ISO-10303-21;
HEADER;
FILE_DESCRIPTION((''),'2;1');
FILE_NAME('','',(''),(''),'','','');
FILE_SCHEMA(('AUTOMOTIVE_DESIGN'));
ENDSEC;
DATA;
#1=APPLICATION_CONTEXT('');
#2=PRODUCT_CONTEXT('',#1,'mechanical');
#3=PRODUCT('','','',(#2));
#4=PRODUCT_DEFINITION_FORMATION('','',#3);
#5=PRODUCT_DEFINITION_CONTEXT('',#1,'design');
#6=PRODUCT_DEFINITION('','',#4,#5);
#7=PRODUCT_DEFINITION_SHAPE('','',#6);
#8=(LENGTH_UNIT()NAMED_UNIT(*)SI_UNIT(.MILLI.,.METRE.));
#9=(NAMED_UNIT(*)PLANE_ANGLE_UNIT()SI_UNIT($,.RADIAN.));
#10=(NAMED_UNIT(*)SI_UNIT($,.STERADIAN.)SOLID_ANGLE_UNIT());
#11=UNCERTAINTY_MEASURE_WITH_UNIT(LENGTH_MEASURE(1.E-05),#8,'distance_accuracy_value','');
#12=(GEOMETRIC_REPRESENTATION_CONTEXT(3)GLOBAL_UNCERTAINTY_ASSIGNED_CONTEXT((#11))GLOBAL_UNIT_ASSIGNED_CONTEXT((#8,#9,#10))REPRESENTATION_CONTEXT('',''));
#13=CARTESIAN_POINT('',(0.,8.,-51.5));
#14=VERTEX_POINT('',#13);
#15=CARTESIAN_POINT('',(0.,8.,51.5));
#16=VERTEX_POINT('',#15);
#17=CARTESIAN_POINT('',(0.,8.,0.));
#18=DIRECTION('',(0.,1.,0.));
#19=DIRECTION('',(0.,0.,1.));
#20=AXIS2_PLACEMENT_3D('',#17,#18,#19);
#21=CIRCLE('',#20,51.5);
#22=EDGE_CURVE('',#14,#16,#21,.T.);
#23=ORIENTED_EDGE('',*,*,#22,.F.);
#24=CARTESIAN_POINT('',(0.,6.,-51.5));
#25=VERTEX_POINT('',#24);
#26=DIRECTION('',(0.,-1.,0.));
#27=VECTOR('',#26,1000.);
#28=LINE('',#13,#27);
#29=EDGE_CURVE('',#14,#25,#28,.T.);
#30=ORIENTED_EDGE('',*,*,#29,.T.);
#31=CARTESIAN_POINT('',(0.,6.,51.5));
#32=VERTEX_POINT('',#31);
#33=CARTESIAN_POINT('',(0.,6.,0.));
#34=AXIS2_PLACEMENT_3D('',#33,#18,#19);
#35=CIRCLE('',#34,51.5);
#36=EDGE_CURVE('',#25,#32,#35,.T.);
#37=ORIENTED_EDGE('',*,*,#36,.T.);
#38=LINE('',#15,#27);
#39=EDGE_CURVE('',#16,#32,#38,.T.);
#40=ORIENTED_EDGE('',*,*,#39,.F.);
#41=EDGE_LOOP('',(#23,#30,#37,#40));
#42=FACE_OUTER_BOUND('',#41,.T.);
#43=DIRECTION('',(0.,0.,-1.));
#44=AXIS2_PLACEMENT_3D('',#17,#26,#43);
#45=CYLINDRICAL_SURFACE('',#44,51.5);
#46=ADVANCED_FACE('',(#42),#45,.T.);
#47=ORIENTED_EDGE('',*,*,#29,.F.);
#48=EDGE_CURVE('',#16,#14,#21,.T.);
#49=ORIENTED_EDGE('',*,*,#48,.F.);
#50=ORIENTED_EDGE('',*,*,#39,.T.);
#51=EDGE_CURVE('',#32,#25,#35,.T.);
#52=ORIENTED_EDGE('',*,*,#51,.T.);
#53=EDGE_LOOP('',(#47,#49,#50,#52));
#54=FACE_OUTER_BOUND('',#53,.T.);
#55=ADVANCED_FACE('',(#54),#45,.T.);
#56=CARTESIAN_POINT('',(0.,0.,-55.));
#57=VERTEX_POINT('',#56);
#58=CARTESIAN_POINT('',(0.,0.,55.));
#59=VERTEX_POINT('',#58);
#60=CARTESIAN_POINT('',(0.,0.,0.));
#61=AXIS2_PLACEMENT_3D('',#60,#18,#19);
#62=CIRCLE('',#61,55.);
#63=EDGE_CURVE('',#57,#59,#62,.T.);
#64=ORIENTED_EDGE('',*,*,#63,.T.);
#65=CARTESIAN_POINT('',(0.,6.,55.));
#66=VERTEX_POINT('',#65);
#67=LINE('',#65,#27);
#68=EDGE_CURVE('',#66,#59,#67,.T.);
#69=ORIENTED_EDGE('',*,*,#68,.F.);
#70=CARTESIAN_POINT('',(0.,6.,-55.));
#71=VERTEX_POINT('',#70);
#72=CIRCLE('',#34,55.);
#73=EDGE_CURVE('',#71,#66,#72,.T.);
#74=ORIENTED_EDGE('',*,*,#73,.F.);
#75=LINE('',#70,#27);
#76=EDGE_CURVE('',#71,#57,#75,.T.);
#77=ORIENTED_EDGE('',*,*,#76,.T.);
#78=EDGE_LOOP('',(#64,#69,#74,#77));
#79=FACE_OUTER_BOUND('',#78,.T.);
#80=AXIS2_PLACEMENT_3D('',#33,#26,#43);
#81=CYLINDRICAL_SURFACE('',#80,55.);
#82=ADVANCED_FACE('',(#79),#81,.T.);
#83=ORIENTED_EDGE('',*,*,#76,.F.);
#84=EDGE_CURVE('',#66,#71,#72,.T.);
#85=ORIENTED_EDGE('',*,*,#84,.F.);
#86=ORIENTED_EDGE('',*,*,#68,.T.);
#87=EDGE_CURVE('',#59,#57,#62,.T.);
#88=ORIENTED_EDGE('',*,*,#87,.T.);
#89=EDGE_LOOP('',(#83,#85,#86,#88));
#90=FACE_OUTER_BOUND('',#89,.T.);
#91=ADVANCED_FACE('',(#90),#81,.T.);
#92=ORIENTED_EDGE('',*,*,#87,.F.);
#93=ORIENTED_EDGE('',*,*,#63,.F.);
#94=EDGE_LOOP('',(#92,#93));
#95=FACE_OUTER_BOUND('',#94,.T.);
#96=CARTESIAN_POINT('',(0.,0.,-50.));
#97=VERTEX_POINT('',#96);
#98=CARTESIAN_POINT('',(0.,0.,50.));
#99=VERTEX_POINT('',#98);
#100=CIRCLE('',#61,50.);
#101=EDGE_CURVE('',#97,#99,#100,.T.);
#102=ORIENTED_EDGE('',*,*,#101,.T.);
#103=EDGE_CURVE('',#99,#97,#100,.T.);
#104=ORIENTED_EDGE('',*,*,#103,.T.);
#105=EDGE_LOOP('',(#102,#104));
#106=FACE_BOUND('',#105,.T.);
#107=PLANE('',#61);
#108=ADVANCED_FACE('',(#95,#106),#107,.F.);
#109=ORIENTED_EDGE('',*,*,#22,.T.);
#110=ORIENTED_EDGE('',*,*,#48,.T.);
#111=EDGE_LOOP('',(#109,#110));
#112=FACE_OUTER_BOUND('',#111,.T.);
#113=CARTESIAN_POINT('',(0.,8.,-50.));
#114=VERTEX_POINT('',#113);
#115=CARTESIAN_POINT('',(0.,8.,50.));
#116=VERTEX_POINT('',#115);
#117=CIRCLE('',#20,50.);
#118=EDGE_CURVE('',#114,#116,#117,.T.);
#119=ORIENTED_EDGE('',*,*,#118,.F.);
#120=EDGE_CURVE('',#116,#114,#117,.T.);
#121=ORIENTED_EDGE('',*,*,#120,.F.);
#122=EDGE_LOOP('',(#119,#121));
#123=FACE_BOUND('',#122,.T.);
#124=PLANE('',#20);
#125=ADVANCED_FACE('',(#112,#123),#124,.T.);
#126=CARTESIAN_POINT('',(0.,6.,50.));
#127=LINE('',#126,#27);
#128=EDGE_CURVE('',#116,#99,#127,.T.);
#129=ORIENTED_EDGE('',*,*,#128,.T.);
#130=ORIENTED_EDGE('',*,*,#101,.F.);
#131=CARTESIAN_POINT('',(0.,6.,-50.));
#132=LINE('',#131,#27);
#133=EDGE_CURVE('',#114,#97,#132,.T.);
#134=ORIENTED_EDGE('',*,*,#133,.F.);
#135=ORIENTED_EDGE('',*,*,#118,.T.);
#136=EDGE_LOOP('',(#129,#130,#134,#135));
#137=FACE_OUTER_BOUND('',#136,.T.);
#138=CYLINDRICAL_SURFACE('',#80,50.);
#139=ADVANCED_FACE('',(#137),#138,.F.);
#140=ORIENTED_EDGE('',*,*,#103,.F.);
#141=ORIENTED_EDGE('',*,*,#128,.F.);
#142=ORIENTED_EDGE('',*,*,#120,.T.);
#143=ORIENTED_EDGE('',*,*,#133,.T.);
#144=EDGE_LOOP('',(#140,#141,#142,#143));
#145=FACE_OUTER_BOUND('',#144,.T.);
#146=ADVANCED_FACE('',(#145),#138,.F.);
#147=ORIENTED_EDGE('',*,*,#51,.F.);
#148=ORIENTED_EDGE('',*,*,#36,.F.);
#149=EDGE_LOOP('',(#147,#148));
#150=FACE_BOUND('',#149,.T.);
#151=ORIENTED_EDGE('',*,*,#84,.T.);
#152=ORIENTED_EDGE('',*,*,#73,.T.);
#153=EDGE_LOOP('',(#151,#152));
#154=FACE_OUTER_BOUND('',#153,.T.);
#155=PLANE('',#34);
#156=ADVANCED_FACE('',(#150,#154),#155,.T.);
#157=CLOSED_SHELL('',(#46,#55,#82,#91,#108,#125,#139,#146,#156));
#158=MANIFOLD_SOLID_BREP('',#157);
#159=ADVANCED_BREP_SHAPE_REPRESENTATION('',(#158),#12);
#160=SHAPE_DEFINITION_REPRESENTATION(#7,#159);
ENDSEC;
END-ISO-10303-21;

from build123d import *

# Parameters (mm, degrees)
SKETCH1_R           = 55
SKETCH1_R_2         = 50
BOSS_EXTRUDE1_DEPTH = 6
SKETCH2_R           = 51.5
SKETCH2_R_2         = 50
BOSS_EXTRUDE2_DEPTH = 2


with BuildPart() as part:
    # Sketch1 → Boss-Extrude1 (new body)
    with BuildSketch(Plane(origin=(0, 0, 0), x_dir=(1, 0, 0), z_dir=(0, 1, 0))):
        with Locations(Location((0, 0, 0), (0, 0, 270))):
            Circle(SKETCH1_R)
        with Locations(Location((0, 0, 0), (0, 0, 270))):
            Circle(SKETCH1_R_2, mode=Mode.SUBTRACT)
    extrude(amount=BOSS_EXTRUDE1_DEPTH)

    # Sketch2 → Boss-Extrude2 (add)
    with BuildSketch(Plane(origin=(0, 6, 0), x_dir=(1, 0, 0), z_dir=(0, 1, 0))):
        with Locations(Location((0, 0, 0), (0, 0, 270))):
            Circle(SKETCH2_R)
        with Locations(Location((0, 0, 0), (0, 0, 270))):
            Circle(SKETCH2_R_2, mode=Mode.SUBTRACT)
    extrude(amount=BOSS_EXTRUDE2_DEPTH)


solid = part.part
